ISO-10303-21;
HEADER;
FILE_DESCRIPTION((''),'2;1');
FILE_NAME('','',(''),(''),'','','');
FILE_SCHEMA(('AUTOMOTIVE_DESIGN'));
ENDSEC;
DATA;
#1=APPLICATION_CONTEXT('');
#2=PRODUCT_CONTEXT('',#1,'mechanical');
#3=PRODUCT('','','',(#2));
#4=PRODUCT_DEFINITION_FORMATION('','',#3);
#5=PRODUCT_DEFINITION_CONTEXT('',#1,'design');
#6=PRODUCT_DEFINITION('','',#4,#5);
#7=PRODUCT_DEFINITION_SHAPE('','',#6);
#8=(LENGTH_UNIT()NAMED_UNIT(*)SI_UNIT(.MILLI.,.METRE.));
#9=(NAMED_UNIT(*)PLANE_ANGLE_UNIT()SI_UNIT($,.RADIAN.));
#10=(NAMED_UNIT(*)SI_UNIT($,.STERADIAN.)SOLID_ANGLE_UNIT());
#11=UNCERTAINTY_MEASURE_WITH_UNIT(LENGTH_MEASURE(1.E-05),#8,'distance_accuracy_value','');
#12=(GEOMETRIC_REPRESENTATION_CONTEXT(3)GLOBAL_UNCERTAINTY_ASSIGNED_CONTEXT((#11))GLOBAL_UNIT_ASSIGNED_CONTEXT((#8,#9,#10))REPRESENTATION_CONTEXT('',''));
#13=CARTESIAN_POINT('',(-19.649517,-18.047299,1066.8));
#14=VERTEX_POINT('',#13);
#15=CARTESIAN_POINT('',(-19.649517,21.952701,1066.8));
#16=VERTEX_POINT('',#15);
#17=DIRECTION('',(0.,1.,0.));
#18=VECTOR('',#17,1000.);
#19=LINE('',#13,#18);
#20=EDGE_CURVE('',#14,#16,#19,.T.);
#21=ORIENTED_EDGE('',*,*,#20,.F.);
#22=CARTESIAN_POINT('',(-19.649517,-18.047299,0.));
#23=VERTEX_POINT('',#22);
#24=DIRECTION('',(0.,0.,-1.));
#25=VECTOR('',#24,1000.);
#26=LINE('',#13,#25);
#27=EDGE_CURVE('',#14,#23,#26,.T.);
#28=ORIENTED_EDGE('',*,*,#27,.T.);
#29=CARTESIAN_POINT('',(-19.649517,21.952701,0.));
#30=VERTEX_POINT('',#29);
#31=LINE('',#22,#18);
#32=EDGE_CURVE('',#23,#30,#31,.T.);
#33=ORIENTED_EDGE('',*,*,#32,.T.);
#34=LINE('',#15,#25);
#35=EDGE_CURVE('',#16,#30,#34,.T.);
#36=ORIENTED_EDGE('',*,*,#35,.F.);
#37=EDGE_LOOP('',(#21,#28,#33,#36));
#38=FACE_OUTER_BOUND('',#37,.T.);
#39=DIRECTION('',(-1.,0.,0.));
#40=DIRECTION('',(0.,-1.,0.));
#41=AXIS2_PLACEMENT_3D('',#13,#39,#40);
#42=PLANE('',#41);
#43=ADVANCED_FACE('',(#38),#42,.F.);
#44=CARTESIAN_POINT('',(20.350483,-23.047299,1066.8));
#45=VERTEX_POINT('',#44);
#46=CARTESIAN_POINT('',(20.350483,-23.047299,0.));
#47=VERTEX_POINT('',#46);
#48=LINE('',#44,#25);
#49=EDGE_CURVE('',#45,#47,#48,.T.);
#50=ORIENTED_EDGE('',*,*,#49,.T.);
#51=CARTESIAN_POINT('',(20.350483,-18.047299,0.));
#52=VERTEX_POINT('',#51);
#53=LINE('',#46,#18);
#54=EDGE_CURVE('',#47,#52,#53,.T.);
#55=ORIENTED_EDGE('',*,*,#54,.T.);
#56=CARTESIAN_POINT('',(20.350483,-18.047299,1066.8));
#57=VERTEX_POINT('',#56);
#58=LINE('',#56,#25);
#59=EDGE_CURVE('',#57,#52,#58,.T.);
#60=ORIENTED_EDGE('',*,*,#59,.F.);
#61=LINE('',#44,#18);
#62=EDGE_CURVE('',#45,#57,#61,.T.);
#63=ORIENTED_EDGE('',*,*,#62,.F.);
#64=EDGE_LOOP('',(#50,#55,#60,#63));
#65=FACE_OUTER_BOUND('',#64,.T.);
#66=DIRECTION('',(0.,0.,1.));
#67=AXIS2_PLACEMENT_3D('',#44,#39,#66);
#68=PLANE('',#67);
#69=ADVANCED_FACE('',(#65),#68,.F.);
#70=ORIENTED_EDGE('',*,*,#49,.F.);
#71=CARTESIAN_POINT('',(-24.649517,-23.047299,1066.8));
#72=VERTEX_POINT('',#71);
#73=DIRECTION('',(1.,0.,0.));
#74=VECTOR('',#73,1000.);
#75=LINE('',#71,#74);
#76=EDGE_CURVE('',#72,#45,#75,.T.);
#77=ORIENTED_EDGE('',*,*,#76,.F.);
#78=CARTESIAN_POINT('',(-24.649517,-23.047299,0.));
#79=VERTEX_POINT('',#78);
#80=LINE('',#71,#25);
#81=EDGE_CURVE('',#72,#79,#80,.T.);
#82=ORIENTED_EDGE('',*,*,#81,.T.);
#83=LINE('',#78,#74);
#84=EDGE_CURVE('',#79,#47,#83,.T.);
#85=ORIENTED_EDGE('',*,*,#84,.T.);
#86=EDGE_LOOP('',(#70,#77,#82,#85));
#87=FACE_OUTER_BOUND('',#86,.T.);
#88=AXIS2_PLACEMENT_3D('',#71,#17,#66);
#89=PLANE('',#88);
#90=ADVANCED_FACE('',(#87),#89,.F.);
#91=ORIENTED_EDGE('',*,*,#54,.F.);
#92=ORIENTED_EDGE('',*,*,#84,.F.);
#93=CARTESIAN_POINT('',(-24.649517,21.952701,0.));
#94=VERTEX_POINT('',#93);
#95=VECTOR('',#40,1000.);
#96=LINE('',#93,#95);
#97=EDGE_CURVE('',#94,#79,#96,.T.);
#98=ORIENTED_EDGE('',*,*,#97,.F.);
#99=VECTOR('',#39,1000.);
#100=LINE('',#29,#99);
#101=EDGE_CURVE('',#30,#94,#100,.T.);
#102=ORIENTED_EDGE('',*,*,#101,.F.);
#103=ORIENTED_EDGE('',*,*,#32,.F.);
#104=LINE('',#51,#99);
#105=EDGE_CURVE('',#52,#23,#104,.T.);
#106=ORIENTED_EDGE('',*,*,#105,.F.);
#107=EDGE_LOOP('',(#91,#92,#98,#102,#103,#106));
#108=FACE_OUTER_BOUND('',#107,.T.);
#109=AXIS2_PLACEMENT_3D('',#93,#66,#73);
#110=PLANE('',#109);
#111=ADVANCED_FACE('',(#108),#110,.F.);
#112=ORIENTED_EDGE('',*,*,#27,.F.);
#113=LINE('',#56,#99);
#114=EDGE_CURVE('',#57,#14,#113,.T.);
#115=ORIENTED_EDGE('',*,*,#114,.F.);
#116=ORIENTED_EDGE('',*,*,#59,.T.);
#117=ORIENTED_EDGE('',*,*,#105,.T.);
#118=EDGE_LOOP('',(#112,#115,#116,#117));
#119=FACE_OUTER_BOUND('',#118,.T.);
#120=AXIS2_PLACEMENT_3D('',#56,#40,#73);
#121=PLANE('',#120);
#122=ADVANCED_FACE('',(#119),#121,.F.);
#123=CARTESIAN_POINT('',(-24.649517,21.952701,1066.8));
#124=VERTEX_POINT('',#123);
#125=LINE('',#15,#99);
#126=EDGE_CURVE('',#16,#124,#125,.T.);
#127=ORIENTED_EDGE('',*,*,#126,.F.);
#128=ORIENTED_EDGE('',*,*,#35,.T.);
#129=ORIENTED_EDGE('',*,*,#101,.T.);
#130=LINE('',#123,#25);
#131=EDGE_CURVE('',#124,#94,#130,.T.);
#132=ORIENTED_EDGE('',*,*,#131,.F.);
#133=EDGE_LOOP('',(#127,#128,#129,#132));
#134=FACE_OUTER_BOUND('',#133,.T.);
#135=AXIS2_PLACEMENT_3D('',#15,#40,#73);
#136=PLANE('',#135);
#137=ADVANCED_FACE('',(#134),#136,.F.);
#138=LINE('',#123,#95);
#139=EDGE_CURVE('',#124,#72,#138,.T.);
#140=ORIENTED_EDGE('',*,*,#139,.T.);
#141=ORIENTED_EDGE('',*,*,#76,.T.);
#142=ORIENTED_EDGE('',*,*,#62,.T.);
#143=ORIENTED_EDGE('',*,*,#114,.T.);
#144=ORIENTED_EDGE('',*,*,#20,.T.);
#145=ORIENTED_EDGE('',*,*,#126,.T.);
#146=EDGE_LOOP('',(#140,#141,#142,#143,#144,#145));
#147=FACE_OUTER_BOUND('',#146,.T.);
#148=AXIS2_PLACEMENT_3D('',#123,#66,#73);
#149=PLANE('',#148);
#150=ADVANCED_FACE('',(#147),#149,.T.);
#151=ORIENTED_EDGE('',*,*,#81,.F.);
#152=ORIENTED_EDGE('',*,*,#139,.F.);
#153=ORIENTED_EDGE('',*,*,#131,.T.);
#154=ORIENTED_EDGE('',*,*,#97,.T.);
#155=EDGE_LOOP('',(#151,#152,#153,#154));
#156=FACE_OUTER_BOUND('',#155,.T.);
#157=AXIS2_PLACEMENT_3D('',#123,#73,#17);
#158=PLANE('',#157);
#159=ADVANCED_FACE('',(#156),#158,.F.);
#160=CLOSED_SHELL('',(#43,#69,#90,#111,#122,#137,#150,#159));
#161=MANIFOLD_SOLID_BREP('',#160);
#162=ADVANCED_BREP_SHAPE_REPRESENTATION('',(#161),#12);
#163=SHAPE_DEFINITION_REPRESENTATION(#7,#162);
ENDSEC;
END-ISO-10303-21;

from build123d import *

# Parameters (mm, degrees)
EXTRUDE1_DEPTH = 1066.8


with BuildPart() as part:
    # Sketch1 → Extrude1 (new body)
    with BuildSketch(Plane.XY):
        Polygon((-24.649517418, 21.952701214), (-24.649517418, -23.047298786), (20.350482582, -23.047298786), (20.350482582, -18.047298786), (-19.649517418, -18.047298786), (-19.649517418, 21.952701214), align=None)
    extrude(amount=EXTRUDE1_DEPTH)


solid = part.part
